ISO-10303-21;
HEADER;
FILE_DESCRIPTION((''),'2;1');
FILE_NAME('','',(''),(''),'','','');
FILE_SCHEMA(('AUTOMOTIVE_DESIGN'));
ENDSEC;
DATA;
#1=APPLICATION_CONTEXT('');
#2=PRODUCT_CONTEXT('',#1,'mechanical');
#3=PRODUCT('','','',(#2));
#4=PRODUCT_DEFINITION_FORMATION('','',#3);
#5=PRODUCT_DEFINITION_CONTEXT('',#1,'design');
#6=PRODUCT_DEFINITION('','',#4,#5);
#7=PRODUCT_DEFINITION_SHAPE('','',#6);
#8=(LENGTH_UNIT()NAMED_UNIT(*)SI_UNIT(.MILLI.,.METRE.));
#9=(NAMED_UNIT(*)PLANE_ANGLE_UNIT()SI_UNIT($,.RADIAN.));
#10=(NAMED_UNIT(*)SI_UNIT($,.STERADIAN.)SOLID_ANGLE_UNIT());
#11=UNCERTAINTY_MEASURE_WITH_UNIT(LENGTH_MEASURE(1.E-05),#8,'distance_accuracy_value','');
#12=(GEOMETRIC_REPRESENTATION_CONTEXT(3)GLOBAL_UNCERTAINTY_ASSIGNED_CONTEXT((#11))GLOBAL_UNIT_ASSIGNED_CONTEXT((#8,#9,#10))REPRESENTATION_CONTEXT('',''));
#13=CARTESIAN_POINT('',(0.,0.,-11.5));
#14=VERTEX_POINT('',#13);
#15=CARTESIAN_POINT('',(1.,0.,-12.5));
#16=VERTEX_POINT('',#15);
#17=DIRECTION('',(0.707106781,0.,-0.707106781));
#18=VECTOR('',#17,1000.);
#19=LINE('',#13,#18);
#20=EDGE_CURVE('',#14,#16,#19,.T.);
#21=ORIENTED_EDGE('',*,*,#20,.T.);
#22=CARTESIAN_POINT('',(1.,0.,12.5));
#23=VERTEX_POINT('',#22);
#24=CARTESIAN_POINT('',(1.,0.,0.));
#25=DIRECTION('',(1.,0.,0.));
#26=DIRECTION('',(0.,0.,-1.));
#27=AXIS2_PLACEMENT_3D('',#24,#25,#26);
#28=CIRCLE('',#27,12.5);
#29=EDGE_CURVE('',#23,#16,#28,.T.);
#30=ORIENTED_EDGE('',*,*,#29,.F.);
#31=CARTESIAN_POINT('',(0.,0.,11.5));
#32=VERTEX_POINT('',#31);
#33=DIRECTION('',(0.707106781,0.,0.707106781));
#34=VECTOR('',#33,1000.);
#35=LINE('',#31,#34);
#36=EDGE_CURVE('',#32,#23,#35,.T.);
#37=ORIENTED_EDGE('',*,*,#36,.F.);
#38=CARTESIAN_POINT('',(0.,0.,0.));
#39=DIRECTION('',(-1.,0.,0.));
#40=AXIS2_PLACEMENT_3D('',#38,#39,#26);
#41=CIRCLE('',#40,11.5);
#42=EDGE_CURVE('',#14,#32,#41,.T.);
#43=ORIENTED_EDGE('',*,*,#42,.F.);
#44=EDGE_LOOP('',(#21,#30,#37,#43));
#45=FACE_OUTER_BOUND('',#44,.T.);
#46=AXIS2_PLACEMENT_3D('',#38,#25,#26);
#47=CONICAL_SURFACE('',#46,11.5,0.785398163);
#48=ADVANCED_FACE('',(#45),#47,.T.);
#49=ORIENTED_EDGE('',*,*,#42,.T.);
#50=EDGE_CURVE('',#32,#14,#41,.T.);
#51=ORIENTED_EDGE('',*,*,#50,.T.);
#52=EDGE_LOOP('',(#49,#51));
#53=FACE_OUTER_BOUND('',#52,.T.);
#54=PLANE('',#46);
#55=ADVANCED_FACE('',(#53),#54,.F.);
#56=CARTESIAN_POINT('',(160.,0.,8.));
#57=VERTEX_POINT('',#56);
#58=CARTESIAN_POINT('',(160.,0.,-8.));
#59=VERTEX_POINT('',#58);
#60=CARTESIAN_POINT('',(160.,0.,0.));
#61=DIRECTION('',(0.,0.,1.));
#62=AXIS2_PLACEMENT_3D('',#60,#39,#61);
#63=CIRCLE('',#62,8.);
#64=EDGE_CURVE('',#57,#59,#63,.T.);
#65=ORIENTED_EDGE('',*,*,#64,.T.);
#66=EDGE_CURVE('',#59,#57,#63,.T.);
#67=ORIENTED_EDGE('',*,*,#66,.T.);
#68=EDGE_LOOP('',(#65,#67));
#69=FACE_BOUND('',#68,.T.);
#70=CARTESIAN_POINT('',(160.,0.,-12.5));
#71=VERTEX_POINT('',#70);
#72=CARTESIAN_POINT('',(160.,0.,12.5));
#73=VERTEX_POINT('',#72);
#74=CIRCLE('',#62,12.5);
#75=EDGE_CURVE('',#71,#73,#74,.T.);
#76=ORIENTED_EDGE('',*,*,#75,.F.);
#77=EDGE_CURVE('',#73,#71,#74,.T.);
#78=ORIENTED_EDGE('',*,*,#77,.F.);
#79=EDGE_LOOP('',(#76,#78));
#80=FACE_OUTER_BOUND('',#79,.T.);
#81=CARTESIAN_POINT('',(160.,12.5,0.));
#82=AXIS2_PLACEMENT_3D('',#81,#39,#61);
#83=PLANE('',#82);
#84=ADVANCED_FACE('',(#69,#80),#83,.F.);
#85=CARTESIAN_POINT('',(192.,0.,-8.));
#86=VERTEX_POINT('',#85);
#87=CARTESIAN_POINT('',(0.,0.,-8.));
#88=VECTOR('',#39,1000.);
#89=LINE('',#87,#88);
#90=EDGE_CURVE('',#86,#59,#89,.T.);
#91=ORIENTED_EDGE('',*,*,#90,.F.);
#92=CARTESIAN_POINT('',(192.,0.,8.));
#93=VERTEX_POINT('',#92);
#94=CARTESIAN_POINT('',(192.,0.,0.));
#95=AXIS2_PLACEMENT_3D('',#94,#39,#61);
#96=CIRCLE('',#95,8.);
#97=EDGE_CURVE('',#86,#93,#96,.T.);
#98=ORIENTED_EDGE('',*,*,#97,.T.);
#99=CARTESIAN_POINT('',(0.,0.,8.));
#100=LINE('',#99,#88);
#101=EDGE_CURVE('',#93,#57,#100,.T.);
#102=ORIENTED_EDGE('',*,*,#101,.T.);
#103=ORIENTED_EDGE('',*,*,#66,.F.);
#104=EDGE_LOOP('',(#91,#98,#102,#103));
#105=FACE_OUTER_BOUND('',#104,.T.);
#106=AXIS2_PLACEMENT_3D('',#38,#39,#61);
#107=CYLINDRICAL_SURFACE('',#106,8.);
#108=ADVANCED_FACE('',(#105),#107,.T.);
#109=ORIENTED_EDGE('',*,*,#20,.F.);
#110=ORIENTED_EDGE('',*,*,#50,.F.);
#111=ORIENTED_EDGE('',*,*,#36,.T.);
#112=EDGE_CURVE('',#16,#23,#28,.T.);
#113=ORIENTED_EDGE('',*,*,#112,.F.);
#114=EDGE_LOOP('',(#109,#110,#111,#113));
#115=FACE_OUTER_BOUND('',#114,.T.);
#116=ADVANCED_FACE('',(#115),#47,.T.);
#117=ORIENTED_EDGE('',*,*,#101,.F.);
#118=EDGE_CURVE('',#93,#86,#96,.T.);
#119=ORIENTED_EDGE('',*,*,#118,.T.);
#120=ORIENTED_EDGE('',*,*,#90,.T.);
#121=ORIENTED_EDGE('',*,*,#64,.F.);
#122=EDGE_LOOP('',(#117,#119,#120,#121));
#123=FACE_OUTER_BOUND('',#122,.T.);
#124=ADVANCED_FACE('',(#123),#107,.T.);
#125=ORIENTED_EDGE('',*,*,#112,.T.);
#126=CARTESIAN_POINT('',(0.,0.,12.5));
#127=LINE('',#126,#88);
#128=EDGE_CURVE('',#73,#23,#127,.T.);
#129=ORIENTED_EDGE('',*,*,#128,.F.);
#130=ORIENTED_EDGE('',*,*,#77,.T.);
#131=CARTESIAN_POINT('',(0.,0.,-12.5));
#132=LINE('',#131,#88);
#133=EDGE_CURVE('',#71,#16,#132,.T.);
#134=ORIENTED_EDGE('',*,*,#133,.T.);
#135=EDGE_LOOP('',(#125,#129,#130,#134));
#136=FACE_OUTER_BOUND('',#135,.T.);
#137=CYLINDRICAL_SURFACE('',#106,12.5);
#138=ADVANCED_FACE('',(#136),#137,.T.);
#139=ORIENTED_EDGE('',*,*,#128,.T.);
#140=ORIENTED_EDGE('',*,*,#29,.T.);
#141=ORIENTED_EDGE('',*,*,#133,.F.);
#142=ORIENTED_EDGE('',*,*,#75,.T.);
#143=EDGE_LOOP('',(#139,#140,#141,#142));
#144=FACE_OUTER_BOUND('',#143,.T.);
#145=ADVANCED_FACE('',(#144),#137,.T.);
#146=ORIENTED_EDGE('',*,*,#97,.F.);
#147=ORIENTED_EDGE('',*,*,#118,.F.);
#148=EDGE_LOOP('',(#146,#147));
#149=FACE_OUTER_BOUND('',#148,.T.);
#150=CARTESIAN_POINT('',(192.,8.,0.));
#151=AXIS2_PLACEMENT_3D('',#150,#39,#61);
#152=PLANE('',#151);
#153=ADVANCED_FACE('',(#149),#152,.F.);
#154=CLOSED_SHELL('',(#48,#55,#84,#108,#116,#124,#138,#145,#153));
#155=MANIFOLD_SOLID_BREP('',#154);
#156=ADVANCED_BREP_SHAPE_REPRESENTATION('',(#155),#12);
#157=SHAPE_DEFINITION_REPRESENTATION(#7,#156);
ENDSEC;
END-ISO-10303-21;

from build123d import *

# Parameters (mm, degrees)
CHAMFER1_SIZE = 1


with BuildPart() as part:
    # Sketch1 → Revolve1 (revolve)
    with BuildSketch(Plane.XY, mode=Mode.PRIVATE) as revolve1_sk:
        Polygon((0, 0), (0, 12.5), (160, 12.5), (160, 8), (192, 8), (192, 0), align=None)
    revolve(revolve1_sk.sketch.rotate(Axis((0, 0, 0), (1, 0, 0)), 90), axis=Axis((0, 0, 0), (1, 0, 0)))

    # Chamfer1
    chamfer1_edges = [part.edges().sort_by_distance(p)[0] for p in [
        (0, 0, -12.5),
    ]]
    chamfer(chamfer1_edges, length=CHAMFER1_SIZE)


solid = part.part
